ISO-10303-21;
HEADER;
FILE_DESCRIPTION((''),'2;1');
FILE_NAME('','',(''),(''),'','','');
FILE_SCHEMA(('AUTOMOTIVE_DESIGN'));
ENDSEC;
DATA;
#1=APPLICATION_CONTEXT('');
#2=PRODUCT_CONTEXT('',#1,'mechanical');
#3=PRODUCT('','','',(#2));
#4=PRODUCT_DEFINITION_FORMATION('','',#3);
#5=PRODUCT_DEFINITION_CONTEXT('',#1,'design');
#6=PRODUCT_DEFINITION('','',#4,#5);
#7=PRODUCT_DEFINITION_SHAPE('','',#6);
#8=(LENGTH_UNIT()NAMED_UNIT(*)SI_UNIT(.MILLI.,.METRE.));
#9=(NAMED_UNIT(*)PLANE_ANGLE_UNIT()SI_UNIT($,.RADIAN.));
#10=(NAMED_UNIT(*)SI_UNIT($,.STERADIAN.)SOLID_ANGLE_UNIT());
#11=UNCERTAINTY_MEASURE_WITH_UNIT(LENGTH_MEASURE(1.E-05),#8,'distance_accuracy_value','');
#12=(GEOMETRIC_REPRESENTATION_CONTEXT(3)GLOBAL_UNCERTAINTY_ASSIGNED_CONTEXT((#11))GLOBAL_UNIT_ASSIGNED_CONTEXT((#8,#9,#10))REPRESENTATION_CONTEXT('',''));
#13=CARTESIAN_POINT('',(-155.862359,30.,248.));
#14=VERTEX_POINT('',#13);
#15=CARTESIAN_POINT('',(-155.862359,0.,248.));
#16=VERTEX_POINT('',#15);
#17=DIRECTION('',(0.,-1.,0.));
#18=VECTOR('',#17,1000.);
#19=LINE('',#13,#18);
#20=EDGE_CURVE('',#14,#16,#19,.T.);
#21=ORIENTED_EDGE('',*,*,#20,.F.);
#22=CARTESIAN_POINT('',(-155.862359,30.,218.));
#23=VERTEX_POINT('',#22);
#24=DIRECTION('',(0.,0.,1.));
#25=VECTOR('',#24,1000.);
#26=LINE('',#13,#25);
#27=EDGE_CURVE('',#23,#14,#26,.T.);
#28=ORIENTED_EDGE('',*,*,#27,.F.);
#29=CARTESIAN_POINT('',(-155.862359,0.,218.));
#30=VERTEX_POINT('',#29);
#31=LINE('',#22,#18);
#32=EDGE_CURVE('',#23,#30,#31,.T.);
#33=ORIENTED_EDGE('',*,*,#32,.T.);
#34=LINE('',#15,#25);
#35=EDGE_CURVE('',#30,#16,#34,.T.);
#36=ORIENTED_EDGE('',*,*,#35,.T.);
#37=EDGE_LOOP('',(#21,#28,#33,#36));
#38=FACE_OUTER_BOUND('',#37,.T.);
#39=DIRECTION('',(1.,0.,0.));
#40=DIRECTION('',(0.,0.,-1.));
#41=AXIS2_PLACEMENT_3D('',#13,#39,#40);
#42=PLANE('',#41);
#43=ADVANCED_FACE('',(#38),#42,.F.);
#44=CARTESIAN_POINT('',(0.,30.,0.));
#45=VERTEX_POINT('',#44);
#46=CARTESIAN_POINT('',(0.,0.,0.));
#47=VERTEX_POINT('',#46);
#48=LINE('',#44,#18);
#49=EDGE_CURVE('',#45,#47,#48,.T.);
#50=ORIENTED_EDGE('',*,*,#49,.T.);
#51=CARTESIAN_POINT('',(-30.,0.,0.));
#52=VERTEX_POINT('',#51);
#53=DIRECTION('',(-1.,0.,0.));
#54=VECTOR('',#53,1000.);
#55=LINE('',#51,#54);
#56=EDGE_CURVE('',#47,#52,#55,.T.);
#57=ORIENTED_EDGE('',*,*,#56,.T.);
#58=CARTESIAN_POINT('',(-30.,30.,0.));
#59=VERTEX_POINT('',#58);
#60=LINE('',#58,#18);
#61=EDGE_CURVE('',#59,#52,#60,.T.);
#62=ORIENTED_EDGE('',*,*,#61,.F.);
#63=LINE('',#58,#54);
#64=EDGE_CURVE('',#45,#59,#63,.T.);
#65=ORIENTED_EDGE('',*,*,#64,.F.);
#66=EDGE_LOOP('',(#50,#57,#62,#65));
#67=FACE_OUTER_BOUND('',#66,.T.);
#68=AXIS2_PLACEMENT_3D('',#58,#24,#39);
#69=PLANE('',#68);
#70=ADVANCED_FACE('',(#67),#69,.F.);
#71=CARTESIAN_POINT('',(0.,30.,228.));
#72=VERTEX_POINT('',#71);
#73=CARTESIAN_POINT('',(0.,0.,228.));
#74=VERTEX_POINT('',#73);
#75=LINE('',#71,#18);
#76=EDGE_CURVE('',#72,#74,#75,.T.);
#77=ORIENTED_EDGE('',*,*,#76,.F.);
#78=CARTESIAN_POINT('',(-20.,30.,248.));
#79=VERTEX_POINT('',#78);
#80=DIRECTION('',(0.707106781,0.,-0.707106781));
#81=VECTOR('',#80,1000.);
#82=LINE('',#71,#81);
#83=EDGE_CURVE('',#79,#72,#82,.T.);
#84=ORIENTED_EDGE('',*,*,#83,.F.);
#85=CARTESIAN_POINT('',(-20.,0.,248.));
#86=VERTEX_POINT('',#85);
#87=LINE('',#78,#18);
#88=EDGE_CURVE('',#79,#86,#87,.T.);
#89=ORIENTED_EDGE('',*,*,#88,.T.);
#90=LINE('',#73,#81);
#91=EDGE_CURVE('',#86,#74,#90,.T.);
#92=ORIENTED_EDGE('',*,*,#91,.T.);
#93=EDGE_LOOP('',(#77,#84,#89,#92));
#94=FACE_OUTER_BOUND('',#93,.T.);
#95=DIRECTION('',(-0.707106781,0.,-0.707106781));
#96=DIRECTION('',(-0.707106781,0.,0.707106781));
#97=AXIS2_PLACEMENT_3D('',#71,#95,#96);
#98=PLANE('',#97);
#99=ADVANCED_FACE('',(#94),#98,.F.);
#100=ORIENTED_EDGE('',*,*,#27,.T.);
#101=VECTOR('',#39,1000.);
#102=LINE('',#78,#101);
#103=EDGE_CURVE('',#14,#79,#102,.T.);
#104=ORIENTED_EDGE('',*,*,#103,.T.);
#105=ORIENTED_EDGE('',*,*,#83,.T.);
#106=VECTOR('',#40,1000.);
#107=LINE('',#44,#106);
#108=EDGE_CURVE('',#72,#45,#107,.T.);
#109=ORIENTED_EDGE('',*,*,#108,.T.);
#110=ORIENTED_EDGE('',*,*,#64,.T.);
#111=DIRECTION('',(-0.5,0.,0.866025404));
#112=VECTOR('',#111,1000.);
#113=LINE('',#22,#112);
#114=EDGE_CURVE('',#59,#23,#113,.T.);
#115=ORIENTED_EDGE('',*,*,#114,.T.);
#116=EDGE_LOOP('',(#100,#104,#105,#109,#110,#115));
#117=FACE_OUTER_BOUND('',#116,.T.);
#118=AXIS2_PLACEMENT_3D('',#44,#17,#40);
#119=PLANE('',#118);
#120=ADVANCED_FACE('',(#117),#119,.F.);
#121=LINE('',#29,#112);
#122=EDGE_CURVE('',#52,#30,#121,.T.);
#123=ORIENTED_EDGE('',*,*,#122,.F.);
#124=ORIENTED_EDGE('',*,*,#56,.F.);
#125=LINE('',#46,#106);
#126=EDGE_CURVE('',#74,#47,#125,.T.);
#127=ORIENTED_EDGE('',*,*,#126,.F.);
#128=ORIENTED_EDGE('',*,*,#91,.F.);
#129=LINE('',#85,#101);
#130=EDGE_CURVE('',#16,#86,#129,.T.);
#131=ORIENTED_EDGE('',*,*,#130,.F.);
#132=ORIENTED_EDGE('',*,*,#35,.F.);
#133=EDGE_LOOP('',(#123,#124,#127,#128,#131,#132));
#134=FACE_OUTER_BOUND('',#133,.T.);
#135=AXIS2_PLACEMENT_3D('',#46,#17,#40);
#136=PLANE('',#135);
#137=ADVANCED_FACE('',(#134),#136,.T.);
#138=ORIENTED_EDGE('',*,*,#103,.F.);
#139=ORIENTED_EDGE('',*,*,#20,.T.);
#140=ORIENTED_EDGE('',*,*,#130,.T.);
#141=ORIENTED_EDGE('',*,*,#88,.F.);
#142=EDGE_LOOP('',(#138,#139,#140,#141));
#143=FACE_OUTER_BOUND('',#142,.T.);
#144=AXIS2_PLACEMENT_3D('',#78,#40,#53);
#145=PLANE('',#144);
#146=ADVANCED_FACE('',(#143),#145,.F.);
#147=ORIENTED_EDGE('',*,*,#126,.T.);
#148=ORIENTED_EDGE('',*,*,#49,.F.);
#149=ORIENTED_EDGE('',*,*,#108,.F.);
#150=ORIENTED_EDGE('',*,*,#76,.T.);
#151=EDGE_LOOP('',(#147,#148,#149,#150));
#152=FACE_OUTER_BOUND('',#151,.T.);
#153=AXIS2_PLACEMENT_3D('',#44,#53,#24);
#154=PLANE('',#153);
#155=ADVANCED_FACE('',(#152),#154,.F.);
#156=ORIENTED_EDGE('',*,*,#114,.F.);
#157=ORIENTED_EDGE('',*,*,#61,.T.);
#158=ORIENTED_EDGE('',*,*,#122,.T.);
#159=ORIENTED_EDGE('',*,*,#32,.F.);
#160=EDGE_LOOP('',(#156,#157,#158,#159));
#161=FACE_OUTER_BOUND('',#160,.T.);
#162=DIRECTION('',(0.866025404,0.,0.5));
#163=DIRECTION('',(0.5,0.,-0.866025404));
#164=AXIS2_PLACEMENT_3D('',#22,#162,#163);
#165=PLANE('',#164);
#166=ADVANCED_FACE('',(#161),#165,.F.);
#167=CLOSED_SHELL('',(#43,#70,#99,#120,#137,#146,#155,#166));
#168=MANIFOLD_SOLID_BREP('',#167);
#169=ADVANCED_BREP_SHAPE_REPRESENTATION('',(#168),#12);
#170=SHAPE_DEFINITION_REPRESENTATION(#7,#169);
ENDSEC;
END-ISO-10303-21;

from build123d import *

# Parameters (mm, degrees)
EXTRUDE_1_DEPTH = 30


with BuildPart() as part:
    # 草图1 → 凸台-拉伸1 (new body)
    with BuildSketch(Plane(origin=(0, 0, 0), x_dir=(1, 0, 0), z_dir=(0, 1, 0))):
        Polygon((0, 0), (0, -228), (-20, -248), (-155.862358683, -248), (-155.862358683, -218), (-30, 0), align=None)
    extrude(amount=EXTRUDE_1_DEPTH)


solid = part.part
